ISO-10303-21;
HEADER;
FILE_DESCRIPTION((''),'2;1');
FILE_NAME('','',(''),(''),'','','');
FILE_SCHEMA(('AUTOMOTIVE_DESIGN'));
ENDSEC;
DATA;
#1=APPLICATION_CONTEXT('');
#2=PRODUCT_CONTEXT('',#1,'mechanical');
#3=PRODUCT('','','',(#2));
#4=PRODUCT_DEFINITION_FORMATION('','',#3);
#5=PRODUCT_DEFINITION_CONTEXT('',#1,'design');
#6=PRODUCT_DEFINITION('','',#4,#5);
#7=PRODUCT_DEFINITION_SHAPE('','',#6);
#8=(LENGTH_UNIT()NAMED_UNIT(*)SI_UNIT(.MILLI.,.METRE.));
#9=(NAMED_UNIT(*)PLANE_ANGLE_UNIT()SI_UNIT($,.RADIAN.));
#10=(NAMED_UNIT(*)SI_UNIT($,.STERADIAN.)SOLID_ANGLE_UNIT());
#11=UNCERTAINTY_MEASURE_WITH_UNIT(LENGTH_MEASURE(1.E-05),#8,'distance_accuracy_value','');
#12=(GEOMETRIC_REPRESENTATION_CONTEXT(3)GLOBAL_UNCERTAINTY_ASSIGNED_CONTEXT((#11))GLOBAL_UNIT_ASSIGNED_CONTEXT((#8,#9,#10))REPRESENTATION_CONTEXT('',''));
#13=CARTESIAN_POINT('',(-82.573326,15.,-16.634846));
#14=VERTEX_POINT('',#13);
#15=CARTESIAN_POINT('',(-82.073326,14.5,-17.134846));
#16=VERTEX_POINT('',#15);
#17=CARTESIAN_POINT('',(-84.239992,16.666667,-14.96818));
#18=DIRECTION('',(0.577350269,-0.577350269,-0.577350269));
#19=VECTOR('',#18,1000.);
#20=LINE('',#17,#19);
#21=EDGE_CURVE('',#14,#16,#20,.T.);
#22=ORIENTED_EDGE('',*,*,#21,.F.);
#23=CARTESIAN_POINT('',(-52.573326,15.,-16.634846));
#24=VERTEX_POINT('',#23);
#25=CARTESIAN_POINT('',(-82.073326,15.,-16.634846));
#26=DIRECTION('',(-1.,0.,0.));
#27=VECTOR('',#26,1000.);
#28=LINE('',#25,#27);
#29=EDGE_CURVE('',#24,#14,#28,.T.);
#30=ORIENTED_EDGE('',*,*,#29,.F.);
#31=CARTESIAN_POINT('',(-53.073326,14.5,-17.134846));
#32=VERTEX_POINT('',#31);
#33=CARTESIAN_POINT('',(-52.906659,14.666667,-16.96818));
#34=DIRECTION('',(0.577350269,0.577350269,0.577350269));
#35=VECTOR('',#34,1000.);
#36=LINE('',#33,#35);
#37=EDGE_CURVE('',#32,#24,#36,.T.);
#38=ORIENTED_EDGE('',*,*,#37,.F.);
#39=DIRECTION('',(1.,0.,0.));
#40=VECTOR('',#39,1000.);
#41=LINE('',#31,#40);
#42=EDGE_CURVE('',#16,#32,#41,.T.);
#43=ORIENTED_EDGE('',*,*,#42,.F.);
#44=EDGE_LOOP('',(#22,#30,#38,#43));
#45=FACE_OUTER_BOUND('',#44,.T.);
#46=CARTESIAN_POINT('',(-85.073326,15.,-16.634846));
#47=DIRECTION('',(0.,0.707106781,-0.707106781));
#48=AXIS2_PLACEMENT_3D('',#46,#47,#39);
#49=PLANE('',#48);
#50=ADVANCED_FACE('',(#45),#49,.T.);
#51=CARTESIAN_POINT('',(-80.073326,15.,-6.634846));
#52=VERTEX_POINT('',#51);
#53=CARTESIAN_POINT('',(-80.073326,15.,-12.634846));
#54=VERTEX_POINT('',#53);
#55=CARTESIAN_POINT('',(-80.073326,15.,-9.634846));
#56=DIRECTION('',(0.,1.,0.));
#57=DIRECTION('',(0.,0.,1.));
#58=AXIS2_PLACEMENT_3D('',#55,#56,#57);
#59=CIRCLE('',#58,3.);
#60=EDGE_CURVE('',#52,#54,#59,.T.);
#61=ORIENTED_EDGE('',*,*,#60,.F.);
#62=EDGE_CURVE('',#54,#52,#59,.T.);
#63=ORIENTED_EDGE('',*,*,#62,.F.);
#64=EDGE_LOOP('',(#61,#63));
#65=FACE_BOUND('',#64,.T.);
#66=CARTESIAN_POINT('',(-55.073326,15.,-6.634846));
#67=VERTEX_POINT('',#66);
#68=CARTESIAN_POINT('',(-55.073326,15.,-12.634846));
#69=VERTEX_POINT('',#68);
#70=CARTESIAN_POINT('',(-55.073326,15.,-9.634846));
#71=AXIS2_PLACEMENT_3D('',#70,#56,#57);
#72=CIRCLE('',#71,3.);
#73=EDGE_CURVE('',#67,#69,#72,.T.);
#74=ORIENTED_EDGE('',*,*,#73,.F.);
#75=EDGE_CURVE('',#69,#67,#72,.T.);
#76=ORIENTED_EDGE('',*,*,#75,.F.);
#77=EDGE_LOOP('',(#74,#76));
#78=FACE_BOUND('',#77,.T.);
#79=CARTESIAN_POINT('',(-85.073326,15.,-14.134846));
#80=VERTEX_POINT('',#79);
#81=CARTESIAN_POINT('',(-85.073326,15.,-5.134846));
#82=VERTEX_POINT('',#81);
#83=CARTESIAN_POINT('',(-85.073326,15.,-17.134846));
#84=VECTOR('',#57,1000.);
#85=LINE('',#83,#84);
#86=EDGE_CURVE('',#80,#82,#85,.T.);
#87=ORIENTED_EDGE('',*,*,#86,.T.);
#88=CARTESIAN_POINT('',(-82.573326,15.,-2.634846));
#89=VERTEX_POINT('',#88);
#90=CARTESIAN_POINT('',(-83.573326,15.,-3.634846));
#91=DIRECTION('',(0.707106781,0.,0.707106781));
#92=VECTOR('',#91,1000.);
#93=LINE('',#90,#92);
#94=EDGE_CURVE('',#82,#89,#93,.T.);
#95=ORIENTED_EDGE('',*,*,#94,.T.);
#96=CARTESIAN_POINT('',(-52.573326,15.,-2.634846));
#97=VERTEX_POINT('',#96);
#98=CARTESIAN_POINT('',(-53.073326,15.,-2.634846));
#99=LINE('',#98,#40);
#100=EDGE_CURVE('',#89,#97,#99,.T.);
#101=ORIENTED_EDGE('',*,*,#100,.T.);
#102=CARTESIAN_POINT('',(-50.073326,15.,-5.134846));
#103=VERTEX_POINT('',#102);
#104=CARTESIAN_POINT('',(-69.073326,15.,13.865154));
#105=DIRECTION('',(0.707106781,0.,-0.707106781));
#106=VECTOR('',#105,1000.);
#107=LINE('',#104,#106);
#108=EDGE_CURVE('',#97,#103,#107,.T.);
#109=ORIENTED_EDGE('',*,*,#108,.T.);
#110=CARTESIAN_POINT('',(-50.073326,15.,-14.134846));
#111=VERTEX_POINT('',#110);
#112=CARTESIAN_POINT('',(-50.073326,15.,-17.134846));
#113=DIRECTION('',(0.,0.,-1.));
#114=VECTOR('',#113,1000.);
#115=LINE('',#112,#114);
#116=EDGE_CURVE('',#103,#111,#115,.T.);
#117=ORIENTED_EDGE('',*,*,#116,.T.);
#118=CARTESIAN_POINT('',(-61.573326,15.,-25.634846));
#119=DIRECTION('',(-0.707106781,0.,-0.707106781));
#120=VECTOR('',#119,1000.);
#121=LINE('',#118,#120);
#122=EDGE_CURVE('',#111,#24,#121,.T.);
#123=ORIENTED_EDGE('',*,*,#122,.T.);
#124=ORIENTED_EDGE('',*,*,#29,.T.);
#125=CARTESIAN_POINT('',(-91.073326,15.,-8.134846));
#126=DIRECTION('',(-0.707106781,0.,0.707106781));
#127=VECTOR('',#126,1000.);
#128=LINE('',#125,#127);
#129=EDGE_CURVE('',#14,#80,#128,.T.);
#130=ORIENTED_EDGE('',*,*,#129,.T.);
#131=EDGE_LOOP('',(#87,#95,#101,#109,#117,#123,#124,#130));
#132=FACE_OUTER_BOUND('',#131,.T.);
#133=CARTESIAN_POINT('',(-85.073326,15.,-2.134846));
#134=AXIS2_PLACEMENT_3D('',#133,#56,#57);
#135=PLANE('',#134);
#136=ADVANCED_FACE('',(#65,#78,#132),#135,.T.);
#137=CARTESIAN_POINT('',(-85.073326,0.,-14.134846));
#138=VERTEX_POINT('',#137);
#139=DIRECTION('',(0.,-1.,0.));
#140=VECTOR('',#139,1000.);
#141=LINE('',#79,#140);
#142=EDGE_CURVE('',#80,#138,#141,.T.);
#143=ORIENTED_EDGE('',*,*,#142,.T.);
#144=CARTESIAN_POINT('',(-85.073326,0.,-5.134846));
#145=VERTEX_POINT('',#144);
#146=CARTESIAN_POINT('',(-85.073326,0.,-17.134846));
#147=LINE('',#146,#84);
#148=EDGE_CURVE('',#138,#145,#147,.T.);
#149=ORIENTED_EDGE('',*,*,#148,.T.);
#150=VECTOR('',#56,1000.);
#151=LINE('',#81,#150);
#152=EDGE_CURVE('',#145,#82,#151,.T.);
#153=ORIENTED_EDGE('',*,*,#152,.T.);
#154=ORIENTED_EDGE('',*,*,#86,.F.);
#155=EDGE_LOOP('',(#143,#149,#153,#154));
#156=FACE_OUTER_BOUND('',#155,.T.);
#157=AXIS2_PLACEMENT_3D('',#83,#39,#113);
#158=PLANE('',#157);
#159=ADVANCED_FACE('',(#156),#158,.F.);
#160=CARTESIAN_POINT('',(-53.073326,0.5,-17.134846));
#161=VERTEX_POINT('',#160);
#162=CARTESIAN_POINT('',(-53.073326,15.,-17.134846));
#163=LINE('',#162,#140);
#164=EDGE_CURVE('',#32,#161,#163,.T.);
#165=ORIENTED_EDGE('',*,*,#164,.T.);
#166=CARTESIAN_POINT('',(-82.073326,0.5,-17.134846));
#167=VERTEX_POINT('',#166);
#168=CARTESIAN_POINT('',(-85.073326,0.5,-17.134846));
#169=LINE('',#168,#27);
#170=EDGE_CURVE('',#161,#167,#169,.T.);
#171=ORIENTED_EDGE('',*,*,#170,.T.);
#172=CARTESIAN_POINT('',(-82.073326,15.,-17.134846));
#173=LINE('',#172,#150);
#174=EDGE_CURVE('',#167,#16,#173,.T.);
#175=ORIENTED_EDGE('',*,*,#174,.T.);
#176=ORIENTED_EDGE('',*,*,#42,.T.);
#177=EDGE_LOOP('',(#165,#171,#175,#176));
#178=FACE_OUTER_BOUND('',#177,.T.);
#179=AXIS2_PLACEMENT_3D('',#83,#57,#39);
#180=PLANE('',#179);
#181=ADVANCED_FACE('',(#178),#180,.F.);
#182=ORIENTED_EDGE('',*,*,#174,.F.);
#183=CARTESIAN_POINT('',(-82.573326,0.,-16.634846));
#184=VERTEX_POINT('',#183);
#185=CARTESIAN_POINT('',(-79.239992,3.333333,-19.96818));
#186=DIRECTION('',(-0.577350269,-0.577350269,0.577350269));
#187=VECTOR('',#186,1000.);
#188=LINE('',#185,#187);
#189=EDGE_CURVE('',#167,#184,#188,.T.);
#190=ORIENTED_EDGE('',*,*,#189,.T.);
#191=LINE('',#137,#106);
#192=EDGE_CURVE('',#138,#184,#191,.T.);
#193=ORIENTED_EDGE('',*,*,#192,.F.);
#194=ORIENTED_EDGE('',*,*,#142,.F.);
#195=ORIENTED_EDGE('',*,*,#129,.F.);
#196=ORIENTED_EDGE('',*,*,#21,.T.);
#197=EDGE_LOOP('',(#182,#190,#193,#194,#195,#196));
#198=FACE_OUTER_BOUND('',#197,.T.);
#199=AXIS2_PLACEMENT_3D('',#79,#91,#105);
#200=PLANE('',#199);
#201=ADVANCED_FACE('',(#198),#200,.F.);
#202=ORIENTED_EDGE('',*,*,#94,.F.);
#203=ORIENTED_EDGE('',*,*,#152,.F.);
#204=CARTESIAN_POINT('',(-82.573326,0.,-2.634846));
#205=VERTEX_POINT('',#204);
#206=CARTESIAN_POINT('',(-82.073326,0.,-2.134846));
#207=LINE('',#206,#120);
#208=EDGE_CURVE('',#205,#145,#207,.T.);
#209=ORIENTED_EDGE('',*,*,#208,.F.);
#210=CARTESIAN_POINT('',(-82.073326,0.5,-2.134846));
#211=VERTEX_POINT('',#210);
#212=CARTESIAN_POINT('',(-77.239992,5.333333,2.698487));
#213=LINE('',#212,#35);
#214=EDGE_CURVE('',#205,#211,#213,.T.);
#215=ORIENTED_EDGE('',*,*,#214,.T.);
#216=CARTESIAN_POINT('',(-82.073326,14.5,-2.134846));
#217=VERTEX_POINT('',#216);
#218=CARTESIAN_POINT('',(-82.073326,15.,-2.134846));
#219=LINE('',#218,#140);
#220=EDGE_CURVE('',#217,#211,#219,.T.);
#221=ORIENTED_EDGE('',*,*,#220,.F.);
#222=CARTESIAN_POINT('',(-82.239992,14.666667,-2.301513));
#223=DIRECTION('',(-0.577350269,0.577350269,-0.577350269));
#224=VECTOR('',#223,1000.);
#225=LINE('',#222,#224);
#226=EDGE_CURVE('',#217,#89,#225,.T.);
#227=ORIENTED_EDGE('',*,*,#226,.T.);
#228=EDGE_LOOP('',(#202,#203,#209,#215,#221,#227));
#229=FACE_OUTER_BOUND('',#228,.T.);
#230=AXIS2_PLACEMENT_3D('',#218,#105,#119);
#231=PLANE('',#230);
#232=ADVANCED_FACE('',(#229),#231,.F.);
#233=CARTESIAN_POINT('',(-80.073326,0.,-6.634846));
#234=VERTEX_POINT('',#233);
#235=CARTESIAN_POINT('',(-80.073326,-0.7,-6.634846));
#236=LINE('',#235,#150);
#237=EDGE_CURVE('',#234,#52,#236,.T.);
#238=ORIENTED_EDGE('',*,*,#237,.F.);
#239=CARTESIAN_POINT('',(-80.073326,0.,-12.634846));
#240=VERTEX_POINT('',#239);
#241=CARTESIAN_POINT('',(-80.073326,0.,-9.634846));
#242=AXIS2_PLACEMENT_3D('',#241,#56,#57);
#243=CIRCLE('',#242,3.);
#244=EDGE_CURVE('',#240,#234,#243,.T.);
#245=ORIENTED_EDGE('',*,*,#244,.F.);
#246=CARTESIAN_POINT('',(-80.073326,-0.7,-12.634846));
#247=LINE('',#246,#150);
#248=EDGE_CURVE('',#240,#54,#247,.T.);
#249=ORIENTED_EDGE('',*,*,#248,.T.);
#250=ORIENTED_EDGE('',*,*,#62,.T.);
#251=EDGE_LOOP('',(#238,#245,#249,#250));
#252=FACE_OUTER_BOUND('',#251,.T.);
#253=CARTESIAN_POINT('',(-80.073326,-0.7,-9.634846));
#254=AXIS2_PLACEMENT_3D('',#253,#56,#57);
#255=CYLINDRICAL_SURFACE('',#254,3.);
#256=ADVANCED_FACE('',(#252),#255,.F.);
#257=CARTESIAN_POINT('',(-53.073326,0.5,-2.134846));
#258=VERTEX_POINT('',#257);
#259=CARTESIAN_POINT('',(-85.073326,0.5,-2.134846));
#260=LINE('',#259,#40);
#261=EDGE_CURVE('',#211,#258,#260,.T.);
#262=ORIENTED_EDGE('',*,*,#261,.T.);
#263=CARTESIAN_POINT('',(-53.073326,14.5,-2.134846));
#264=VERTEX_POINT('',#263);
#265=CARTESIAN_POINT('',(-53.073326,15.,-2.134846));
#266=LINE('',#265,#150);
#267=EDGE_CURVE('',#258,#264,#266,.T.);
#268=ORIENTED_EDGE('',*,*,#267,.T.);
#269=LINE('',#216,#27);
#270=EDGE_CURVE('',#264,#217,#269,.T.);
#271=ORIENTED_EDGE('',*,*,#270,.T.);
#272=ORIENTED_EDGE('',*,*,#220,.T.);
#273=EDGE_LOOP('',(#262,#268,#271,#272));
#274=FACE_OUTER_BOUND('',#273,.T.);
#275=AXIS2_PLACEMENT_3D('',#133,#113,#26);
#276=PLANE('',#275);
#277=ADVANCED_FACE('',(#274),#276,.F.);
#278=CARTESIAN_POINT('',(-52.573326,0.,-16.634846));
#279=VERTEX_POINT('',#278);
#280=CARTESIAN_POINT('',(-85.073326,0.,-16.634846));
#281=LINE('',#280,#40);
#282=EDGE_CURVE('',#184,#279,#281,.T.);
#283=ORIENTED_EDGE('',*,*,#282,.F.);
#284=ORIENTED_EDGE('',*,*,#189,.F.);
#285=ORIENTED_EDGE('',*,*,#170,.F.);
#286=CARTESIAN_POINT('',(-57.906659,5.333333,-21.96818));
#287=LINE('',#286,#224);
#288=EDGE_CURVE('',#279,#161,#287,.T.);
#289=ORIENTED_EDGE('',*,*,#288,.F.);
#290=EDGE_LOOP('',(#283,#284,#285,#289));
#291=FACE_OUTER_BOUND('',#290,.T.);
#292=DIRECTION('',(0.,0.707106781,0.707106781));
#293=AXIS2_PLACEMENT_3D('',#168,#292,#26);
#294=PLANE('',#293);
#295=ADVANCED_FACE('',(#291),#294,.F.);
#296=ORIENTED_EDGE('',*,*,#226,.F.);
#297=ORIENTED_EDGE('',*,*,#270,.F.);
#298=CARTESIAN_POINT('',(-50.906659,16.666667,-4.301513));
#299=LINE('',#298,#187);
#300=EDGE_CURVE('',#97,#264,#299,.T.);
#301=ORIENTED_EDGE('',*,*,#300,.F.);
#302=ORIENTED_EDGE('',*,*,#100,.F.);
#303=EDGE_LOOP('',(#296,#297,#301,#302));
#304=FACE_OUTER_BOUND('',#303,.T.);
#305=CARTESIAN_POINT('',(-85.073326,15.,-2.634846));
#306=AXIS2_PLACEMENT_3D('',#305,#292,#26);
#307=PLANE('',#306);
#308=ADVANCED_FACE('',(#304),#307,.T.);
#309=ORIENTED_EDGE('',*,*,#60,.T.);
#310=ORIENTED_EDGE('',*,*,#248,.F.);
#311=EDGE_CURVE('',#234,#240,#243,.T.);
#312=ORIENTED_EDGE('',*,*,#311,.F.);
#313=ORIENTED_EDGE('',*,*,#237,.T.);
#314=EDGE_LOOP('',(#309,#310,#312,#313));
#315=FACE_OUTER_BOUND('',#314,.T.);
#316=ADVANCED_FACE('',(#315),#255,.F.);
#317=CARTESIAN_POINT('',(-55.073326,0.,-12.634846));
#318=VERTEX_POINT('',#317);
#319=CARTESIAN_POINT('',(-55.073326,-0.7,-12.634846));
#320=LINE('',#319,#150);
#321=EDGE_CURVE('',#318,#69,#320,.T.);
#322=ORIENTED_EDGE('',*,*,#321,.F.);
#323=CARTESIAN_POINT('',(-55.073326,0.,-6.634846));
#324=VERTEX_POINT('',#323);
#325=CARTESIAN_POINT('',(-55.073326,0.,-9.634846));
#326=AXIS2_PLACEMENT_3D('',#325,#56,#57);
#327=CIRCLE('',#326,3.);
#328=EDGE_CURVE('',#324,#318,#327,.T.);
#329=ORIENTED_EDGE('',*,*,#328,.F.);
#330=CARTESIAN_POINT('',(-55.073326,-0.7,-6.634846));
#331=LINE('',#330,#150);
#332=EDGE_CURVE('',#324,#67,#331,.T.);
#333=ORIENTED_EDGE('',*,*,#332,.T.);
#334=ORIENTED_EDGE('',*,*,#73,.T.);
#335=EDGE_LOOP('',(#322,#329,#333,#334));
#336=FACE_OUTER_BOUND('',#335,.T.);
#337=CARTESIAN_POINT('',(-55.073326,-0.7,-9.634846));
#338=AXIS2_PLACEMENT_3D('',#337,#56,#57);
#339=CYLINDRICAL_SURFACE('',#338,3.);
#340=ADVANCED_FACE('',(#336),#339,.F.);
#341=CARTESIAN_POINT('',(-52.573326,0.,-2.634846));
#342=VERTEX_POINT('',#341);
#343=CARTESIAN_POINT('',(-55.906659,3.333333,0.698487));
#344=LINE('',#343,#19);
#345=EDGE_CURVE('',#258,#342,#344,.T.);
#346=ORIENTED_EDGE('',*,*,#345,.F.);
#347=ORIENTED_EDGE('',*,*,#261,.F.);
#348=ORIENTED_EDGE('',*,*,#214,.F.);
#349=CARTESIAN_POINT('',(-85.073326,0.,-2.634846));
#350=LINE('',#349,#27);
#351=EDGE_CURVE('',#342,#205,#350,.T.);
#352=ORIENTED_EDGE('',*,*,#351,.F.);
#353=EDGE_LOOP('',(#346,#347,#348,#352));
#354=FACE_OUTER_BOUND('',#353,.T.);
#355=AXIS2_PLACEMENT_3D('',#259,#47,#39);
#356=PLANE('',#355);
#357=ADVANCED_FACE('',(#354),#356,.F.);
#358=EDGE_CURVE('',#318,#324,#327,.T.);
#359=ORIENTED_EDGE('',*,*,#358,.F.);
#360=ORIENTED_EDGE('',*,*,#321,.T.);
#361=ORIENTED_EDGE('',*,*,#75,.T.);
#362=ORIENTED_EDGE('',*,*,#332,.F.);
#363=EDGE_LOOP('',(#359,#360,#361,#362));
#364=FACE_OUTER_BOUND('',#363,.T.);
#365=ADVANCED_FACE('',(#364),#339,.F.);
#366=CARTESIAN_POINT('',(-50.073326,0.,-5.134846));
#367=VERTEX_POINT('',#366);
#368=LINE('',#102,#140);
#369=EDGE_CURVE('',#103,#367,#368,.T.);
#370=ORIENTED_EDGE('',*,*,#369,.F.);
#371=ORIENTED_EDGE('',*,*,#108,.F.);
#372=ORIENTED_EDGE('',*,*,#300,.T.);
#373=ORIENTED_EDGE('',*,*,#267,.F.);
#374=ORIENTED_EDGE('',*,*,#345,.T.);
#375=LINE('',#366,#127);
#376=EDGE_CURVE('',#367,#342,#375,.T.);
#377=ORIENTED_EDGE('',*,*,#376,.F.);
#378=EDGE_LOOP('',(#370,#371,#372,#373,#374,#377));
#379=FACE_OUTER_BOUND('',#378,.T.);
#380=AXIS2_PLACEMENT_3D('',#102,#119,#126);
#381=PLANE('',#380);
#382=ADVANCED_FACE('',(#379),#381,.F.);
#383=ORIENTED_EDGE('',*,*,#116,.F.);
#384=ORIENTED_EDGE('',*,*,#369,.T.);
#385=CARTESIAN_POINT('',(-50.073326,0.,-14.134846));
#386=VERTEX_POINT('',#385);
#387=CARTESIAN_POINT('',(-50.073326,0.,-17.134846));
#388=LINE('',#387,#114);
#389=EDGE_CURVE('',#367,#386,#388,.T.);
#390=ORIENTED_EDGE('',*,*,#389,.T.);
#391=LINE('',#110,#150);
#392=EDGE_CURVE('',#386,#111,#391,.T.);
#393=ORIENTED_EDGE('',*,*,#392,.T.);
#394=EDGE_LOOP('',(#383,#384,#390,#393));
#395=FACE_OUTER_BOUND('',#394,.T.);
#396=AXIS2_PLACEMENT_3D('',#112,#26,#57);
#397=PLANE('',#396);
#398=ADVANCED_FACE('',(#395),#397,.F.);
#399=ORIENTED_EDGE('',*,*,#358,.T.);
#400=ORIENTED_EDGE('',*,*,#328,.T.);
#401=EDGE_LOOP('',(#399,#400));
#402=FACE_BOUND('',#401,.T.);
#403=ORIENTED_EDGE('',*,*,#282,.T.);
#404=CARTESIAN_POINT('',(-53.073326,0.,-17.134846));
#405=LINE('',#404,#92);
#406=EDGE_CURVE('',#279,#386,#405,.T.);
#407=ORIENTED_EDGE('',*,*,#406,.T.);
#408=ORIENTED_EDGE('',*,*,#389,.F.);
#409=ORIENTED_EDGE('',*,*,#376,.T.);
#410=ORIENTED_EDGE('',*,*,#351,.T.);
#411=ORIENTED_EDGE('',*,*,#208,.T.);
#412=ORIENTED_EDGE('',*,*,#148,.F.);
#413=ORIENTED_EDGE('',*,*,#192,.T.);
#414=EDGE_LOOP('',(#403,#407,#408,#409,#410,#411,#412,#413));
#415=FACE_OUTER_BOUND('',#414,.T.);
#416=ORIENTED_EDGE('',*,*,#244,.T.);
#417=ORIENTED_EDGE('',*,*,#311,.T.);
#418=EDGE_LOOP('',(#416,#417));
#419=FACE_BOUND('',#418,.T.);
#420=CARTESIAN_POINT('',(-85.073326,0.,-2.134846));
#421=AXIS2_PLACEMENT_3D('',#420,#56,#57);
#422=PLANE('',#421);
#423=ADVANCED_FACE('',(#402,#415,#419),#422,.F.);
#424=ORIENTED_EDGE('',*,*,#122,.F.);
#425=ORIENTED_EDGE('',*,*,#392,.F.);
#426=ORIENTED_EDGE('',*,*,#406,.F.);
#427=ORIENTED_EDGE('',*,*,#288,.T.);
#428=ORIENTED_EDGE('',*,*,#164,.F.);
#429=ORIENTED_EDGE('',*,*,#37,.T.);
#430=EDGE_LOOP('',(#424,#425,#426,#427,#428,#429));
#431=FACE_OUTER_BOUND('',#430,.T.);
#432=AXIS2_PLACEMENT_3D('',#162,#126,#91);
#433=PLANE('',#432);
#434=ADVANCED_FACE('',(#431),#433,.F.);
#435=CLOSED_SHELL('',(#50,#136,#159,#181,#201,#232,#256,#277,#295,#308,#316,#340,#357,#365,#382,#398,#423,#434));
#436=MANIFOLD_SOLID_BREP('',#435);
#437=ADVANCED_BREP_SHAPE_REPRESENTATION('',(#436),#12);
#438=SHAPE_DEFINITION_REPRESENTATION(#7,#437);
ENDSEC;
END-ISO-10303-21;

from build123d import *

# Parameters (mm, degrees)
SKETCH1_W           = 35
SKETCH1_H           = 15
BOSS_EXTRUDE1_DEPTH = 15
SKETCH2_R           = 3
CUT_EXTRUDE1_DEPTH  = 15.7
CHAMFER1_SIZE       = 3
CHAMFER2_SIZE       = 0.5


with BuildPart() as part:
    # Sketch1 → Boss-Extrude1 (new body)
    with BuildSketch(Plane(origin=(0, 0, 0), x_dir=(1, 0, 0), z_dir=(0, 1, 0))):
        with Locations((-67.573325782, 9.634846385)):
            Rectangle(SKETCH1_W, SKETCH1_H)
    extrude(amount=BOSS_EXTRUDE1_DEPTH)

    # Sketch2 → Cut-Extrude1 (cut)
    with BuildSketch(Plane(origin=(0, 15, 0), x_dir=(1, 0, 0), z_dir=(0, 1, 0))):
        with Locations(Location((-80.073325782, 9.634846385, 0), (0, 0, 270))):
            Circle(SKETCH2_R)
        with Locations(Location((-55.073325782, 9.634846385, 0), (0, 0, 270))):
            Circle(SKETCH2_R)
    extrude(amount=-CUT_EXTRUDE1_DEPTH, mode=Mode.SUBTRACT)

    # Chamfer1
    chamfer1_edges = [part.edges().sort_by_distance(p)[0] for p in [
        (-85.073325782, 7.5, -17.134846385),
        (-50.073325782, 7.5, -17.134846385),
        (-50.073325782, 7.5, -2.134846385),
        (-85.073325782, 7.5, -2.134846385),
    ]]
    chamfer(chamfer1_edges, length=CHAMFER1_SIZE)

    # Chamfer2
    chamfer2_edges = [part.edges().sort_by_distance(p)[0] for p in [
        (-67.573325782, 0, -17.134846385),
        (-67.573325782, 0, -2.134846385),
        (-67.573325782, 15, -2.134846385),
        (-67.573325782, 15, -17.134846385),
    ]]
    chamfer(chamfer2_edges, length=CHAMFER2_SIZE)


solid = part.part
